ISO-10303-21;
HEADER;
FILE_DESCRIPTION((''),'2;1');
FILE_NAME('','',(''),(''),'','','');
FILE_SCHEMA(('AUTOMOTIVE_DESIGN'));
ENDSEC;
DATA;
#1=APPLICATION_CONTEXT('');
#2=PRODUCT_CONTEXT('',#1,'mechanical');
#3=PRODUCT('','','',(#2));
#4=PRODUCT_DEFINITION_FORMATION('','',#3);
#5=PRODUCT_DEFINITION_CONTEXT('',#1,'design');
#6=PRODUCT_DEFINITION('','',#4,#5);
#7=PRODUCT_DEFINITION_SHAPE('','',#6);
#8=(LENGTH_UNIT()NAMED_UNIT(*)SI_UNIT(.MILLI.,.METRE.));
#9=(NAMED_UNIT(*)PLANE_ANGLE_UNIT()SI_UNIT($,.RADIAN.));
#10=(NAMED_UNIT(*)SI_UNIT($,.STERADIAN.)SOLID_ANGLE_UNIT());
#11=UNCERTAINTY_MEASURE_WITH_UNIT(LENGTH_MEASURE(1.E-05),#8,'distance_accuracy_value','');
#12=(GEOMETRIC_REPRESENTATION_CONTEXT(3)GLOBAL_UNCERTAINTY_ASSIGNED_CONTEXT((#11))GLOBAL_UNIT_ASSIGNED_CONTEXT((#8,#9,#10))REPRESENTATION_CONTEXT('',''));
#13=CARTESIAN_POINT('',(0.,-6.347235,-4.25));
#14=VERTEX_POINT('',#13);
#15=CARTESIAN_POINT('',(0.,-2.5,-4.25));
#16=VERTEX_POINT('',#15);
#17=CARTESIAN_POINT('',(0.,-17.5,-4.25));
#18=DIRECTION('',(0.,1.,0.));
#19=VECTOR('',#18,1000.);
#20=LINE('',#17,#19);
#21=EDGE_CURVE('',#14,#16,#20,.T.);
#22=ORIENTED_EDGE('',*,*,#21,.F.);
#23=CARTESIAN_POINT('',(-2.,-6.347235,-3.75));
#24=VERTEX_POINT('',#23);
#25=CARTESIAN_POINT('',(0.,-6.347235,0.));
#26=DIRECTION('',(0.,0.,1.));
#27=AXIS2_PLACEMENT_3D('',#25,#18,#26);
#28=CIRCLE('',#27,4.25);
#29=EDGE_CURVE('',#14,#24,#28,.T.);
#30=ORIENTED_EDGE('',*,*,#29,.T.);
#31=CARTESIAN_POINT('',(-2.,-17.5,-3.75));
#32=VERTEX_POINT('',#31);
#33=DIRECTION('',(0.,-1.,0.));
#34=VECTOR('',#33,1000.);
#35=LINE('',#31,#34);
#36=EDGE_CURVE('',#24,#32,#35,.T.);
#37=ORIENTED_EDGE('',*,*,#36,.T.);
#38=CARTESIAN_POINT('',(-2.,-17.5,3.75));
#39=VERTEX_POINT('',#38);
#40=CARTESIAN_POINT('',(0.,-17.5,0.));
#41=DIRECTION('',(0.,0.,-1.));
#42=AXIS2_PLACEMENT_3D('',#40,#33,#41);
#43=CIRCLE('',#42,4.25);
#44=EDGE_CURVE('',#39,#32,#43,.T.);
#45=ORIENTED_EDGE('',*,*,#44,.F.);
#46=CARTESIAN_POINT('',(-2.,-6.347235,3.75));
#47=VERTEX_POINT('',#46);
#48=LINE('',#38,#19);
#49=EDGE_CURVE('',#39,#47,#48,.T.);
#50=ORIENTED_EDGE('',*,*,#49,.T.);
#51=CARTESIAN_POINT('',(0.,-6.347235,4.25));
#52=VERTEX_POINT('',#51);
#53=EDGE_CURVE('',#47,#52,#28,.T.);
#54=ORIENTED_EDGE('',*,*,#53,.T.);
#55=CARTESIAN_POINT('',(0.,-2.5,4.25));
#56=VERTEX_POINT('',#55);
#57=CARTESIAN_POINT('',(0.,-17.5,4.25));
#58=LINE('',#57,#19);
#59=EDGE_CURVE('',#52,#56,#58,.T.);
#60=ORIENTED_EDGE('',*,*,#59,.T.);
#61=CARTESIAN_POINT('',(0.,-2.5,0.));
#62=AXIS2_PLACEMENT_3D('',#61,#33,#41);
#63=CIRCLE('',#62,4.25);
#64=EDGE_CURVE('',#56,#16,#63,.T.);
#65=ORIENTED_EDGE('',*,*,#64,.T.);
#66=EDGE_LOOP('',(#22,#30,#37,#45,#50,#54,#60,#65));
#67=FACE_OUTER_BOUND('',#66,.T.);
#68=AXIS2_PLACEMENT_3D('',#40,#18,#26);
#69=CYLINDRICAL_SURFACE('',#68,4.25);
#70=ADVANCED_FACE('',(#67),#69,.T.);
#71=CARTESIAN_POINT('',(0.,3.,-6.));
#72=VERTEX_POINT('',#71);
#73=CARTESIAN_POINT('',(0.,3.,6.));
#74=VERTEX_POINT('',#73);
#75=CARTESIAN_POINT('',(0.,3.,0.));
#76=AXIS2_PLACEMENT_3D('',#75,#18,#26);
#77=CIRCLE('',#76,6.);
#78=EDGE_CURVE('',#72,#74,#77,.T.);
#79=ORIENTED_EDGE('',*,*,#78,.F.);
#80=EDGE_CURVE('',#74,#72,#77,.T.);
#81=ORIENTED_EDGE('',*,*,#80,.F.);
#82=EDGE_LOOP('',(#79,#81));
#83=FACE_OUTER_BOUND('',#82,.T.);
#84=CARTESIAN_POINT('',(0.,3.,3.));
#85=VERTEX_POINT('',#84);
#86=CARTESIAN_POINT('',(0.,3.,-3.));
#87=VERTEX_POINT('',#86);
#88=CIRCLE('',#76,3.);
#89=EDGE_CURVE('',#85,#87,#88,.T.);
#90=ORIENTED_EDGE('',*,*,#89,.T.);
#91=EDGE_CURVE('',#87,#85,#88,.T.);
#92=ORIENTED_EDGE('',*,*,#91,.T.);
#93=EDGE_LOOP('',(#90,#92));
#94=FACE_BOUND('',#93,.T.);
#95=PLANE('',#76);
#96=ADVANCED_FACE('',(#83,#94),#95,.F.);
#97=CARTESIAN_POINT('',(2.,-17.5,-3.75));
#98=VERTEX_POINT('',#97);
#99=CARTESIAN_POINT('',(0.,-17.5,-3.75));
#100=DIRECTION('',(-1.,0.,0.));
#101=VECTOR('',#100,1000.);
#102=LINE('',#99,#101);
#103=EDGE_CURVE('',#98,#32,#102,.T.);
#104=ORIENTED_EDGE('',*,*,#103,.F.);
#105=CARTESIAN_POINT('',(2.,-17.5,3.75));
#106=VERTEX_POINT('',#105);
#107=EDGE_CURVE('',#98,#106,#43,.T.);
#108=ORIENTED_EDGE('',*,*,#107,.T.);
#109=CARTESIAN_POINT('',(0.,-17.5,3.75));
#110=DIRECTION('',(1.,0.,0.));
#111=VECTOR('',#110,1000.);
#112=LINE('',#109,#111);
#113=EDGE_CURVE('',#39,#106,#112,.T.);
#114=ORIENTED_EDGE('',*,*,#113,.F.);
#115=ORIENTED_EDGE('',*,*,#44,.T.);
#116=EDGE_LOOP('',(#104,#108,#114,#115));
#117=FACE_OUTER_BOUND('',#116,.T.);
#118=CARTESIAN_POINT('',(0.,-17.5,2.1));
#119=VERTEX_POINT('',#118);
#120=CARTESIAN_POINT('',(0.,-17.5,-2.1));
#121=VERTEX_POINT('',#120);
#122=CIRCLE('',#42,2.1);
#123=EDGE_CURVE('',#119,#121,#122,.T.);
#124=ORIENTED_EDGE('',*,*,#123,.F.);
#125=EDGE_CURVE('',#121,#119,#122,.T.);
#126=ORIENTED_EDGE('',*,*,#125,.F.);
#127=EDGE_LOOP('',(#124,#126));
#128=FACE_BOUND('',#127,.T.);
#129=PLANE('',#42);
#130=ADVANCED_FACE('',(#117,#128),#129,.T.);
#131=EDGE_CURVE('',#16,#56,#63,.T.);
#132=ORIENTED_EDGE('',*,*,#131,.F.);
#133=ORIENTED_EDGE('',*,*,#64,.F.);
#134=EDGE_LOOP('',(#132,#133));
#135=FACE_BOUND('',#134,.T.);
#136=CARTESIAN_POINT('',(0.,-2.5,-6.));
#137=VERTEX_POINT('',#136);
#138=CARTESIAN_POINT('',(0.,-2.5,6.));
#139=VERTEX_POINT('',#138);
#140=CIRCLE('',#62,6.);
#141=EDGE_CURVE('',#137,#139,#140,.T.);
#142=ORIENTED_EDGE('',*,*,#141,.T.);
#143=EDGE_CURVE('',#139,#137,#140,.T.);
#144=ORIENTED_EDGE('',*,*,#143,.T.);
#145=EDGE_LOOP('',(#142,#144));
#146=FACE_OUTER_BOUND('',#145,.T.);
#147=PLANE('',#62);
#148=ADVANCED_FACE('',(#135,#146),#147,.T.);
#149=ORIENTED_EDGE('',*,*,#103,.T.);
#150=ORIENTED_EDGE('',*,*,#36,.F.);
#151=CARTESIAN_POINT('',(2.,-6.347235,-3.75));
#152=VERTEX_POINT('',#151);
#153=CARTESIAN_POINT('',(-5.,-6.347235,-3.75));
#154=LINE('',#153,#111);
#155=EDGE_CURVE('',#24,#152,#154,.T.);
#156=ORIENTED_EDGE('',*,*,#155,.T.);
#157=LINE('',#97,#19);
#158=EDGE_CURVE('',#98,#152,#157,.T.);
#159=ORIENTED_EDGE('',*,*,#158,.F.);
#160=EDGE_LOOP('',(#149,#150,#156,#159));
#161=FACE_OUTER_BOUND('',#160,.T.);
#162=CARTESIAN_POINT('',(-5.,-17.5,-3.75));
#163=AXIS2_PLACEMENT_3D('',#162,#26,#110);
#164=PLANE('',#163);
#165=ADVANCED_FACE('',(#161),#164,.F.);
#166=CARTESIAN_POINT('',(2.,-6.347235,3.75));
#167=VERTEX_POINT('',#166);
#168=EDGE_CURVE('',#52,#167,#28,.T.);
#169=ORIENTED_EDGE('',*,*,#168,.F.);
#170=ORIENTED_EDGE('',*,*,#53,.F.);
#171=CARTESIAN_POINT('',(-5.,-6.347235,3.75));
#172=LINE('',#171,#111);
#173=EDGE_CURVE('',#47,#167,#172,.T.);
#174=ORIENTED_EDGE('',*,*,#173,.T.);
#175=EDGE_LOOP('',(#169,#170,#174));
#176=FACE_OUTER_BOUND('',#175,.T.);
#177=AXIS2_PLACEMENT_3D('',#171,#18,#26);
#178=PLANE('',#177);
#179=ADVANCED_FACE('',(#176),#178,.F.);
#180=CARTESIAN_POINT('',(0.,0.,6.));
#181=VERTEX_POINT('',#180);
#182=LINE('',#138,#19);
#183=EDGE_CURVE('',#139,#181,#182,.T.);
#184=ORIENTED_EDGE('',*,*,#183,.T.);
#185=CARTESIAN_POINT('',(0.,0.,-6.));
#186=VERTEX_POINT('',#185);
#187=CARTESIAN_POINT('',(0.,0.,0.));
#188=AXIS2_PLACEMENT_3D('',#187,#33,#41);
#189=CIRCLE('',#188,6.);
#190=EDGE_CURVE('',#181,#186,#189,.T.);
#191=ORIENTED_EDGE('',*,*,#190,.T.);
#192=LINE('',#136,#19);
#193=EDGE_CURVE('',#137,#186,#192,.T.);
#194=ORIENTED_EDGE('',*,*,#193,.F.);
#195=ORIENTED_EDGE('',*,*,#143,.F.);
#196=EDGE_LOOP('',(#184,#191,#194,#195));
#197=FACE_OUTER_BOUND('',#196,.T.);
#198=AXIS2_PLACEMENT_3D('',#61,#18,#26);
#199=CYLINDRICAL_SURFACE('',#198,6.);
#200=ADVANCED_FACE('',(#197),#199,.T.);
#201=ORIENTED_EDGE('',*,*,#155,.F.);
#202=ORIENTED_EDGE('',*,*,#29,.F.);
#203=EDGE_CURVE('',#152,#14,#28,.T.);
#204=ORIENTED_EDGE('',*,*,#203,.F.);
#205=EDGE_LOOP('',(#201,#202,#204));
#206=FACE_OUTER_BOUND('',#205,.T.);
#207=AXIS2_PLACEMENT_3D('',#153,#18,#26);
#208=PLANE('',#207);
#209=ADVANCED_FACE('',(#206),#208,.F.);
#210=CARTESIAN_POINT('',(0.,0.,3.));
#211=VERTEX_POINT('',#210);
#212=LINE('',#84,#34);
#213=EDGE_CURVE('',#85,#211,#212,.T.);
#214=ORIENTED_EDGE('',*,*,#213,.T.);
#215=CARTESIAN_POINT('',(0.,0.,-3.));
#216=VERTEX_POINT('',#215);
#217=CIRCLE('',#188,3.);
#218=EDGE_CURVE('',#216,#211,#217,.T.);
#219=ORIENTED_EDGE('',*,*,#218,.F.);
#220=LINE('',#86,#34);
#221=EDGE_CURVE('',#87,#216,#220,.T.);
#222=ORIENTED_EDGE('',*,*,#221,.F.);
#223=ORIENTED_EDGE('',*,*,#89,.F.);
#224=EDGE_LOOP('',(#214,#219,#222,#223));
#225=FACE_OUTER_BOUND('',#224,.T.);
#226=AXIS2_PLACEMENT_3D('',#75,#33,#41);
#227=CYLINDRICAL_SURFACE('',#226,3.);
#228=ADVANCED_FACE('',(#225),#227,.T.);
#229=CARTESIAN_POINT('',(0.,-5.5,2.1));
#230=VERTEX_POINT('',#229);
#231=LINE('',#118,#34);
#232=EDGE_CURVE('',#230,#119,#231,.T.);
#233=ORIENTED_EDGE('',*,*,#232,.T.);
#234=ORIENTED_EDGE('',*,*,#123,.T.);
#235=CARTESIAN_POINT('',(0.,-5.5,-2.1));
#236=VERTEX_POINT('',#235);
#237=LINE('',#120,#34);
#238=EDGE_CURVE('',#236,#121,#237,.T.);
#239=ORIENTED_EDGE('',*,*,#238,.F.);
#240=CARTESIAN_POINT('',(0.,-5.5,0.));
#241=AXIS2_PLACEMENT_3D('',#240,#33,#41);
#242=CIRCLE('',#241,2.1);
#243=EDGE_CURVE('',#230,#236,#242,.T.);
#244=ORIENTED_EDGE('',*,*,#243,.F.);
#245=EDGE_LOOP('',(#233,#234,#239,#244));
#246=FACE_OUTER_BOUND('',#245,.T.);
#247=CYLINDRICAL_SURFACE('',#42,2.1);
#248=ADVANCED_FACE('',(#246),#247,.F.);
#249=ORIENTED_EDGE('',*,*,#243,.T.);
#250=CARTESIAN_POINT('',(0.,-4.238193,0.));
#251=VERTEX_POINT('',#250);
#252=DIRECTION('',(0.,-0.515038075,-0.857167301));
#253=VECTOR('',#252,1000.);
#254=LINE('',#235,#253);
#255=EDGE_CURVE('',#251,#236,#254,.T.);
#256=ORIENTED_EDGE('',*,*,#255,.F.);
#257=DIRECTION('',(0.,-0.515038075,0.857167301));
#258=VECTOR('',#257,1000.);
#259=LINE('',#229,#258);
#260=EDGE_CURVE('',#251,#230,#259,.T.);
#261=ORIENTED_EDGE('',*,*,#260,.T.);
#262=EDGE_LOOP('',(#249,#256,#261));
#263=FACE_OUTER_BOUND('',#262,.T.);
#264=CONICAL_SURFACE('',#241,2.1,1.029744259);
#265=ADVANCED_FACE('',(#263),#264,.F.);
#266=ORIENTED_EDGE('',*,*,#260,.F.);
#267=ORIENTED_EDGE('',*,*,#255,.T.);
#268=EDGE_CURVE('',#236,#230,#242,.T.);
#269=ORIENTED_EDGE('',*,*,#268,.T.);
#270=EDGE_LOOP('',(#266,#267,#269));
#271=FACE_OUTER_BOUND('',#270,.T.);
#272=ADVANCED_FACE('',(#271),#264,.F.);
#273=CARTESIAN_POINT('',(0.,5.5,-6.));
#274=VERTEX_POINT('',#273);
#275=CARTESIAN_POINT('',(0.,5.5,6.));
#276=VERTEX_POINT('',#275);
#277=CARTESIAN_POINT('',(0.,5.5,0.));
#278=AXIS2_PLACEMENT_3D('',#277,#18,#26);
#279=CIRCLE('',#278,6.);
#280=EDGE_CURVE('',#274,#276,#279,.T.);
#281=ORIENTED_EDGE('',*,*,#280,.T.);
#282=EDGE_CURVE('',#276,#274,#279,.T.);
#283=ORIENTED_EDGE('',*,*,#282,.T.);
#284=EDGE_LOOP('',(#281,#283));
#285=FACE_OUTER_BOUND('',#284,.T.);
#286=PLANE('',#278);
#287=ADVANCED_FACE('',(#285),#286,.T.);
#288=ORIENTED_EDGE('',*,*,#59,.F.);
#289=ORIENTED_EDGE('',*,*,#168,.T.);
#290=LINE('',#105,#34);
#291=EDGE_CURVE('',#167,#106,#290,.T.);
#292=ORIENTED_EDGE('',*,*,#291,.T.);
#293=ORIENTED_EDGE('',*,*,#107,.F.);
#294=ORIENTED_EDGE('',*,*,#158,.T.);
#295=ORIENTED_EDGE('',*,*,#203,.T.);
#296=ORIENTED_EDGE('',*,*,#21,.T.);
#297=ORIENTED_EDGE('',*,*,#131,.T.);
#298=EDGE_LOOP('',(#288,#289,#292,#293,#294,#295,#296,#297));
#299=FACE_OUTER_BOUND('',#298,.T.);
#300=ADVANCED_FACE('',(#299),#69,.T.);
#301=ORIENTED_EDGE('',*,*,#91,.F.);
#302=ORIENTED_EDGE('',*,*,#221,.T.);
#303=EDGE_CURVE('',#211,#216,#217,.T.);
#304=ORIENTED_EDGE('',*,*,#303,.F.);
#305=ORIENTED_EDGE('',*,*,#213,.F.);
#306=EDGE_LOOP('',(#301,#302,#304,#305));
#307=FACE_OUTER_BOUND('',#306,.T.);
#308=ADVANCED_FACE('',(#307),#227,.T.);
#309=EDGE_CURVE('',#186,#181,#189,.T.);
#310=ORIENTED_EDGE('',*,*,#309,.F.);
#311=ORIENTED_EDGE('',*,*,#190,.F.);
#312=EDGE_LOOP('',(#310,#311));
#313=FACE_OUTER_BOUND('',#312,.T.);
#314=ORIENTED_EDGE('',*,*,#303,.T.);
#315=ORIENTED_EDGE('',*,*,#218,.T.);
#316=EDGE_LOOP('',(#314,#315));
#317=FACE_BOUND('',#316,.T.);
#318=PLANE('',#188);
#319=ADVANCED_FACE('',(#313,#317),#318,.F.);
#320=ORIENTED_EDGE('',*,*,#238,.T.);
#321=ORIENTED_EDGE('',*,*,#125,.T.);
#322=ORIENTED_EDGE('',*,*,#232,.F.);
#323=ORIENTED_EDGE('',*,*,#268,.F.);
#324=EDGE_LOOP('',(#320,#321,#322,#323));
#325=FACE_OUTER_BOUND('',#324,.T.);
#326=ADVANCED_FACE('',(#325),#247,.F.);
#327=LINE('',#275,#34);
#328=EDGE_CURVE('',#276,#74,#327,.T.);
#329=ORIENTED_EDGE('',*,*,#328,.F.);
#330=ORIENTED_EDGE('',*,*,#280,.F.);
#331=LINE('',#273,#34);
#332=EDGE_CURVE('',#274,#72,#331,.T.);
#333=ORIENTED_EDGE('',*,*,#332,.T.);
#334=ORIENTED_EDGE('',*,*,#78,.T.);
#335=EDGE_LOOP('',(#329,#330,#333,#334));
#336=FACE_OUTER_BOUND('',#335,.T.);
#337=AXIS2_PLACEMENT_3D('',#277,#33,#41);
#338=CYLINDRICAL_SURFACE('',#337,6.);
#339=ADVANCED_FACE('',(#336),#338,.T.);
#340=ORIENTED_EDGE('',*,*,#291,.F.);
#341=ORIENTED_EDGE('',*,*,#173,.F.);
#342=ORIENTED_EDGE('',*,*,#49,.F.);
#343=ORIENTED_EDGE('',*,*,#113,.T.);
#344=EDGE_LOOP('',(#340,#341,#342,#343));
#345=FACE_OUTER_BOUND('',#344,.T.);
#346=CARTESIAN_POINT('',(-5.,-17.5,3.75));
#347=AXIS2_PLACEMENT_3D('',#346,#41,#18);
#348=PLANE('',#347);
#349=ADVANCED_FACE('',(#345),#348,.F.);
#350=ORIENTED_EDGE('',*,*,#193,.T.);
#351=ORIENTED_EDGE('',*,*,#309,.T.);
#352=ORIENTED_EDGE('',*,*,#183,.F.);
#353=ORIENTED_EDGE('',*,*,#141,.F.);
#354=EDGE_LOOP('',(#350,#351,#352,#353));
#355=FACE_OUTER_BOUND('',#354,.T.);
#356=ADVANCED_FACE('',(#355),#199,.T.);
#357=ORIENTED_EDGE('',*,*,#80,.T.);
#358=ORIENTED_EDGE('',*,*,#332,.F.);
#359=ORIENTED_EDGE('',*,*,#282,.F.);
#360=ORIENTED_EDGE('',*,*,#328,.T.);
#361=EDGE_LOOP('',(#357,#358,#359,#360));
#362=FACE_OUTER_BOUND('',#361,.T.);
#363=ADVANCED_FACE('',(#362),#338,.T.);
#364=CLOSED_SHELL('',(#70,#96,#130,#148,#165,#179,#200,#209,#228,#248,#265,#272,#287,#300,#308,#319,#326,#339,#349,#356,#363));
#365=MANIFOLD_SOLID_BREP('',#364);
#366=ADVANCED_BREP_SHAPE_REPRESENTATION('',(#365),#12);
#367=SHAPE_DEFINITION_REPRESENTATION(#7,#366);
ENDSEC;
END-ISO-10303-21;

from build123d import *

# Parameters (mm, degrees)
SKETCH1_R             = 3
BOSS_EXTRUDE1_DEPTH   = 3
SKETCH2_R             = 6
BOSS_EXTRUDE2_DEPTH   = 2.5
BOSS_EXTRUDE3_START   = 2.5
SKETCH3_R             = 6
BOSS_EXTRUDE3_DEPTH   = 2.5
SKETCH4_R             = 4.25
BOSS_EXTRUDE4_DEPTH   = 15
SKETCH5_R             = 1
CUT_EXTRUDE1_DEPTH    = 7
M5_TAPPED_HOLE1_D     = 4.2
M5_TAPPED_HOLE1_DEPTH = 12
M5_TAPPED_HOLE1_TIP   = 1.2618073
SKETCH7_W             = 2.207825045
SKETCH7_H             = 11.152764798
CUT_EXTRUDE2_DEPTH    = 5


with BuildPart() as part:
    # Sketch1 → Boss-Extrude1 (new body)
    with BuildSketch(Plane(origin=(0, 0, 0), x_dir=(1, 0, 0), z_dir=(0, 1, 0))):
        with Locations(Location((0, 0, 0), (0, 0, 270))):
            Circle(SKETCH1_R)
    extrude(amount=BOSS_EXTRUDE1_DEPTH)

    # Sketch2 → Boss-Extrude2 (add)
    with BuildSketch(Plane(origin=(0, 3, 0), x_dir=(1, 0, 0), z_dir=(0, 1, 0))):
        with Locations(Location((0, 0, 0), (0, 0, 270))):
            Circle(SKETCH2_R)
    extrude(amount=BOSS_EXTRUDE2_DEPTH)

    # Sketch3 → Boss-Extrude3 (add)
    with BuildSketch(Plane.XZ.offset(BOSS_EXTRUDE3_START)):
        with Locations(Location((0, 0, 0), (0, 0, 90))):
            Circle(SKETCH3_R)
    extrude(amount=-BOSS_EXTRUDE3_DEPTH)

    # Sketch4 → Boss-Extrude4 (add)
    with BuildSketch(Plane.XZ.offset(2.5)):
        with Locations(Location((0, 0, 0), (0, 0, 270))):
            Circle(SKETCH4_R)
    extrude(amount=BOSS_EXTRUDE4_DEPTH)

    # Sketch5 → Cut-Extrude1 (cut)
    with BuildSketch(Plane.XZ.offset(17.5)):
        with Locations(Location((0, 0, 0), (0, 0, 270))):
            Circle(SKETCH5_R)
    extrude(amount=-CUT_EXTRUDE1_DEPTH, mode=Mode.SUBTRACT)

    # M5 Tapped Hole1
    with Locations(Plane(origin=(0, -17.5, 0), x_dir=(0, 0, -1), z_dir=(0, -1, 0))):
        with Locations((0, 0)):
            Hole(M5_TAPPED_HOLE1_D / 2, depth=M5_TAPPED_HOLE1_DEPTH)
            with Locations((0, 0, -(M5_TAPPED_HOLE1_DEPTH + M5_TAPPED_HOLE1_TIP / 2))):  # 118° drill point
                Cone(0, M5_TAPPED_HOLE1_D / 2, M5_TAPPED_HOLE1_TIP, mode=Mode.SUBTRACT)

    # Sketch7 → Cut-Extrude2 (cut, symmetric)
    with BuildSketch(Plane(origin=(0, 0, 0), x_dir=(0, 0, -1), z_dir=(1, 0, 0))):
        with Locations((4.853912523, -11.923617601)):
            Rectangle(SKETCH7_W, SKETCH7_H)
        with Locations((-4.853912523, -11.923617601)):
            Rectangle(SKETCH7_W, SKETCH7_H)
    extrude(amount=CUT_EXTRUDE2_DEPTH, both=True, mode=Mode.SUBTRACT)


solid = part.part
